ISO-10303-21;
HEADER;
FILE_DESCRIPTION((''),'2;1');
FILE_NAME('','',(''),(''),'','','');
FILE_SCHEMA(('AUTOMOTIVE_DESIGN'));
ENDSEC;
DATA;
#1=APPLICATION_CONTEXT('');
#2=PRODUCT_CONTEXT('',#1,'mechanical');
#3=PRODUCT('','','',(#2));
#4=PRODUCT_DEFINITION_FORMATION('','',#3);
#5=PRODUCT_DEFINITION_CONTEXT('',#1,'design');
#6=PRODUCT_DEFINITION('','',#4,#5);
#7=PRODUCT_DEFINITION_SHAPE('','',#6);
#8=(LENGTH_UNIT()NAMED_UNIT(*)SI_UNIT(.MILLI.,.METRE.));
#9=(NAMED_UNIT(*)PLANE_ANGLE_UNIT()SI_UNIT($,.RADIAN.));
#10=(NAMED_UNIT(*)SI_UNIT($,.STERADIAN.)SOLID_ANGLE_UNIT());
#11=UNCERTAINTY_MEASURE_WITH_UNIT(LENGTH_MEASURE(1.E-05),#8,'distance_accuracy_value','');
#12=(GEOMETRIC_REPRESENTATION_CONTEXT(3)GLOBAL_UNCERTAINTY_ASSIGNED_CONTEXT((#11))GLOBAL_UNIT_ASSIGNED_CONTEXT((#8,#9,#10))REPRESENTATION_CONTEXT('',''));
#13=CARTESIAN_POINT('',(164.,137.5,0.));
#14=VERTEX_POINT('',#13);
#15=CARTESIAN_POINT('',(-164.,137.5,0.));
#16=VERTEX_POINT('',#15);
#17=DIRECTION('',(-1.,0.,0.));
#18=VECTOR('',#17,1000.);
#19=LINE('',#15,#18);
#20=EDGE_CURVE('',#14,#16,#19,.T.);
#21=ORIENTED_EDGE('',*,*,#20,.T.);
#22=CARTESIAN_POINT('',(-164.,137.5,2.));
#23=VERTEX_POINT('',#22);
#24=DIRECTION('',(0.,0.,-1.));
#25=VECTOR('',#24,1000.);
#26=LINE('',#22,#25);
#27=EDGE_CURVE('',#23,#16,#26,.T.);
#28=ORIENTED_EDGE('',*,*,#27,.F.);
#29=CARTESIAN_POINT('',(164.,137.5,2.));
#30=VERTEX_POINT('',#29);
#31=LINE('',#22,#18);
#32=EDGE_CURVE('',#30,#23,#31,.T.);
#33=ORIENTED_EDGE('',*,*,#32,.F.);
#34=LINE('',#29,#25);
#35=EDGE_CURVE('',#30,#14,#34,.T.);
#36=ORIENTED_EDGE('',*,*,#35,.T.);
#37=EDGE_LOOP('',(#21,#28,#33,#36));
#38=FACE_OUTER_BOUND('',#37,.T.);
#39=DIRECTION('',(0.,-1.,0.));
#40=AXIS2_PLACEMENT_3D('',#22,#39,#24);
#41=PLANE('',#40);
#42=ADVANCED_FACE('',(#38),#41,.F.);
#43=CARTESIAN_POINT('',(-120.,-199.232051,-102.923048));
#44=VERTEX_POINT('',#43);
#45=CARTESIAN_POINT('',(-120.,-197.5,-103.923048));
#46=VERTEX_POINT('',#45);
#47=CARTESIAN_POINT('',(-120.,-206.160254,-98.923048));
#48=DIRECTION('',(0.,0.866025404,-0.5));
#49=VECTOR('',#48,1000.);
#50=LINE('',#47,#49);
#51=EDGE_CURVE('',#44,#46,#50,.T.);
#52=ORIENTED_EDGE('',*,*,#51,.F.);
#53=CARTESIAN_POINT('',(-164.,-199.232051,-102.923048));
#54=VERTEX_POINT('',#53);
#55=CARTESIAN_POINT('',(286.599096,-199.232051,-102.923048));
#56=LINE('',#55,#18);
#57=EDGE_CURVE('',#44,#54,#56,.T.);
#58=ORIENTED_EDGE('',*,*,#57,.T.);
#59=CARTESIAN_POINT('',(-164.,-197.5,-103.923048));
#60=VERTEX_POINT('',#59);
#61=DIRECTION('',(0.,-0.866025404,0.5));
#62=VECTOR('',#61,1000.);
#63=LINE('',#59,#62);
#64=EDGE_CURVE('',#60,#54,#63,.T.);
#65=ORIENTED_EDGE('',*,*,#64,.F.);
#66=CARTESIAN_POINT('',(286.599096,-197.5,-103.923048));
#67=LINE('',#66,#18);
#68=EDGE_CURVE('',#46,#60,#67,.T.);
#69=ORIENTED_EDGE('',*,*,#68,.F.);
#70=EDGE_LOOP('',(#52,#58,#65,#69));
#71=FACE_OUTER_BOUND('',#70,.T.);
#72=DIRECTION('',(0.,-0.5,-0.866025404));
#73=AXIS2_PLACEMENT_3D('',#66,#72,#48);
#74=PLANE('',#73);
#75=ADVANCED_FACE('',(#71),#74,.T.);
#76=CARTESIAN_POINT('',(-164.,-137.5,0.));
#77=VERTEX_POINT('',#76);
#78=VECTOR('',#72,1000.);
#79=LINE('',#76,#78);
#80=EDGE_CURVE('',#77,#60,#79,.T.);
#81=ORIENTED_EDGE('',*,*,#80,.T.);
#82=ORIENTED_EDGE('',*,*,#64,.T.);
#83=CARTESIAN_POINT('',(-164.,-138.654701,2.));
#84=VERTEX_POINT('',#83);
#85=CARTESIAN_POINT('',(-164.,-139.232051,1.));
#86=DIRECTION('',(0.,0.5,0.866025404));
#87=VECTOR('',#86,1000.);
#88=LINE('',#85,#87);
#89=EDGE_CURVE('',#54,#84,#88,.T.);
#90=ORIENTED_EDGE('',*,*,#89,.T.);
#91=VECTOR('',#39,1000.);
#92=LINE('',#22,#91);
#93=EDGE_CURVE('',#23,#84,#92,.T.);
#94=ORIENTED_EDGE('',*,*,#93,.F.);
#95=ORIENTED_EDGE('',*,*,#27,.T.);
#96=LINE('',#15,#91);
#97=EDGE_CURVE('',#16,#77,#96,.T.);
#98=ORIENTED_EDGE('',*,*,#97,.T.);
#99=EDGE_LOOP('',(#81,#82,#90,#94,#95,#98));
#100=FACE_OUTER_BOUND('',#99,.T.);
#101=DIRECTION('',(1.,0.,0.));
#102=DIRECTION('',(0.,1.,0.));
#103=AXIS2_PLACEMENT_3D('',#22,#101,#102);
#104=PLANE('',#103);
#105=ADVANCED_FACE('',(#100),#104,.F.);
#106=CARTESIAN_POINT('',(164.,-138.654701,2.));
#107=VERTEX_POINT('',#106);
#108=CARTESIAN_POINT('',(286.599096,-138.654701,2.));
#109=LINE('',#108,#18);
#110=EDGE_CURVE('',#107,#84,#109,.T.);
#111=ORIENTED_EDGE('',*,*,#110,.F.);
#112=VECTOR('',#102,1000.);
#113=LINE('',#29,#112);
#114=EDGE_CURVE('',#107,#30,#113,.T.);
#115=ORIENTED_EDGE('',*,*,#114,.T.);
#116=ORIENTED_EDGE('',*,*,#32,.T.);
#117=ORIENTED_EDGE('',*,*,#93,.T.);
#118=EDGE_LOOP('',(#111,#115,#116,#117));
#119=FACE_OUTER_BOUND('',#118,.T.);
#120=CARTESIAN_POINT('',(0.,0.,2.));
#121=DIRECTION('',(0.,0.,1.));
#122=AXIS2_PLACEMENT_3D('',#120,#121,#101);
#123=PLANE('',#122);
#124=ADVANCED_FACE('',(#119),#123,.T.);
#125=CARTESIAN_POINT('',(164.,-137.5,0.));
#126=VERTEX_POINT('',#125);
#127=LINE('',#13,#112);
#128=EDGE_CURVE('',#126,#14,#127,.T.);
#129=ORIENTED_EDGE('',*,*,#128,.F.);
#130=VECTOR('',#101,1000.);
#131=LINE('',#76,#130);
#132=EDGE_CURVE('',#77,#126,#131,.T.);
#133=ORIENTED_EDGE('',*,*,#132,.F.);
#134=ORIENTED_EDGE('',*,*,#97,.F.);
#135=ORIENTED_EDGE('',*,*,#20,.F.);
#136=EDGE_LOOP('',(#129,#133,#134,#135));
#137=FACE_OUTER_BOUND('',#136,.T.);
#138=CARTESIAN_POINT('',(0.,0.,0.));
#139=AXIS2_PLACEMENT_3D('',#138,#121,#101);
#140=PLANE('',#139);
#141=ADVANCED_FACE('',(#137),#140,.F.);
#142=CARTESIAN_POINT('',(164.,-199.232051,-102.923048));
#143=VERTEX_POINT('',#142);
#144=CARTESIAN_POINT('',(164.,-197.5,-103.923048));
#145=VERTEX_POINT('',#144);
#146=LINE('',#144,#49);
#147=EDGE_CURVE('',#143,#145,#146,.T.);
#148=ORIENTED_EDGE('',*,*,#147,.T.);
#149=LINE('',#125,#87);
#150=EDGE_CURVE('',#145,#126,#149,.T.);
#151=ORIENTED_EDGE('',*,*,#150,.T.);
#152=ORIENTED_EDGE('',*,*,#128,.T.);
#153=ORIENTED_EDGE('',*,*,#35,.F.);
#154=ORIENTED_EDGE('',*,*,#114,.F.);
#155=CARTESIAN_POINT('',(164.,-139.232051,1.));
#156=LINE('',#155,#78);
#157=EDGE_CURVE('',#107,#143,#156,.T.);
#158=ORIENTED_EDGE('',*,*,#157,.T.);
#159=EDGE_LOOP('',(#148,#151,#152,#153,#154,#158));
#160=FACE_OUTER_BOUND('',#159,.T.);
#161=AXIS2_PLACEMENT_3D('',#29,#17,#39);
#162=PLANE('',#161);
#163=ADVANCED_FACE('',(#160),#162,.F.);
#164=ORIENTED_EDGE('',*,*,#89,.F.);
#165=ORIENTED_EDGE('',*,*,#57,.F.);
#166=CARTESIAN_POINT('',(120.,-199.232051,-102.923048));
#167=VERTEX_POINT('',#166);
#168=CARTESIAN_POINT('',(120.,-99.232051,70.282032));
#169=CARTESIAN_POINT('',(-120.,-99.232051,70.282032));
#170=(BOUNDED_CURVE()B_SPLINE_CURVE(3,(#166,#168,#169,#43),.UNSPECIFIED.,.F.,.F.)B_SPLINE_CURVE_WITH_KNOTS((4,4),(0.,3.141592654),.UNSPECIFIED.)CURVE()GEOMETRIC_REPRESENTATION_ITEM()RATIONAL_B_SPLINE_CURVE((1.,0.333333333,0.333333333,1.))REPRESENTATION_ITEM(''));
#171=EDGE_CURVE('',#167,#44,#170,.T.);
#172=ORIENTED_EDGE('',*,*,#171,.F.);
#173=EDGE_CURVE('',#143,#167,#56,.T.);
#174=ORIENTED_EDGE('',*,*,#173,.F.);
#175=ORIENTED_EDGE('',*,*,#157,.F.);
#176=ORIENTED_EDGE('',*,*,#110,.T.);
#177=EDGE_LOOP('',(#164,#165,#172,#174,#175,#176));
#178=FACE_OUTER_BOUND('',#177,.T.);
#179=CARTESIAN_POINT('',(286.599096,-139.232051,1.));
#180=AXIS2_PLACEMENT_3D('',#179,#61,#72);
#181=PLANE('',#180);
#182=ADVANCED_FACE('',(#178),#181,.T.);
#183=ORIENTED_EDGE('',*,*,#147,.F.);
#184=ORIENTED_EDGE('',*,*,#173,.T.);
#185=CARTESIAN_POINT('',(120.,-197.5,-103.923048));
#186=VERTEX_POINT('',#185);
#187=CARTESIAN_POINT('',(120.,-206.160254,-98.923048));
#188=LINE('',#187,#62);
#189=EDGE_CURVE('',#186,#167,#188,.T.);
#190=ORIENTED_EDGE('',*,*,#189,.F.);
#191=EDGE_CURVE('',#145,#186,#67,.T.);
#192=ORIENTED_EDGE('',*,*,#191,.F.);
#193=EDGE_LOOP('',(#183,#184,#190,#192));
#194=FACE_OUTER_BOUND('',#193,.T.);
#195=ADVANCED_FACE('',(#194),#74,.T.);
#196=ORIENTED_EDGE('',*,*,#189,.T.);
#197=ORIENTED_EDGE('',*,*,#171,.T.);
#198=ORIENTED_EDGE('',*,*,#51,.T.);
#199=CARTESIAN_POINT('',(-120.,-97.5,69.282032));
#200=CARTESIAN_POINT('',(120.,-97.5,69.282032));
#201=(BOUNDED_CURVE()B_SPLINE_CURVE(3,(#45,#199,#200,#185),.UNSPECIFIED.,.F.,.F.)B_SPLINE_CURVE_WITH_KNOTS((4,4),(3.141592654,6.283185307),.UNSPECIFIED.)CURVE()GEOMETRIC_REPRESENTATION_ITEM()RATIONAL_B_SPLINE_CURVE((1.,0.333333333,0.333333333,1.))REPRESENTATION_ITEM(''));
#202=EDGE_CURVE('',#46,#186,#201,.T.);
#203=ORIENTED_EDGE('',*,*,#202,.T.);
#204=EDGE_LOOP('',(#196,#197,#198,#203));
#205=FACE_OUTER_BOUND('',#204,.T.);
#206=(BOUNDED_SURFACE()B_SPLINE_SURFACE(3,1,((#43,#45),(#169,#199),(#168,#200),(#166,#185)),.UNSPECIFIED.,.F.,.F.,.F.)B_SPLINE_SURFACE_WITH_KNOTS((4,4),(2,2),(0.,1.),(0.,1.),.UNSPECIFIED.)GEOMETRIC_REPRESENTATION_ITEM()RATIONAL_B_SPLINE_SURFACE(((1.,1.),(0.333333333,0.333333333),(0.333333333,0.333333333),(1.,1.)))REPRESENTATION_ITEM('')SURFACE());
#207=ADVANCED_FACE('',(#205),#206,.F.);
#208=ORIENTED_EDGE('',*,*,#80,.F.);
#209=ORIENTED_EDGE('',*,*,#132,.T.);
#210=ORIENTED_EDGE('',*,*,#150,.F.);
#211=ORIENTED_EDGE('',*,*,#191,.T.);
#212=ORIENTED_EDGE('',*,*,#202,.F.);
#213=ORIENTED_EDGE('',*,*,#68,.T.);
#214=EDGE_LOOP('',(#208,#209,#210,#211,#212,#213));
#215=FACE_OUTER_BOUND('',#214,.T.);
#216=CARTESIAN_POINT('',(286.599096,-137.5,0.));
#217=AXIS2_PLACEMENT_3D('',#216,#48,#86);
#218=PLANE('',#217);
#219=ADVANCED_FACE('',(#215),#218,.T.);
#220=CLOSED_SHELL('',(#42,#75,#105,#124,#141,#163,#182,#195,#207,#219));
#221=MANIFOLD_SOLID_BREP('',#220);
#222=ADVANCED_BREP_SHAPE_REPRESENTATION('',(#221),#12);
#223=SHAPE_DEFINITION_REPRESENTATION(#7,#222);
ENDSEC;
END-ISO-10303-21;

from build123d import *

# Parameters (mm, degrees)
SKETCH_1_W          = 328
SKETCH_1_H          = 275
EXTRUDE_1_DEPTH     = 2
EXTRUDE_2_DEPTH     = 328
SKETCH_4_RX         = 120
SKETCH_4_RY         = 100
CUT_EXTRUDE_1_DEPTH = 10


with BuildPart() as part:
    # 草图1 → 凸台-拉伸1 (new body)
    with BuildSketch(Plane.XY):
        Rectangle(SKETCH_1_W, SKETCH_1_H)
    extrude(amount=EXTRUDE_1_DEPTH)

    # 草图2 → 凸台-拉伸2 (add)
    with BuildSketch(Plane.ZY.offset(164)):
        Polygon((0, -137.5), (-103.923048454, -197.5), (-102.923048454, -199.232050808), (1, -139.232050808), (2, -138.654700538), (2, -137.5), align=None)
    extrude(amount=-EXTRUDE_2_DEPTH)

    # 草图4 → 切除-拉伸1 (cut)
    with BuildSketch(Plane(origin=(0, -103.125, 59.53924651), x_dir=(1, 0, 0), z_dir=(0, 0.8660254037844398, -0.49999999999999784))):
        with Locations(Location((0, 188.75), (0, 0, 0))):
            Ellipse(SKETCH_4_RX, SKETCH_4_RY)
    extrude(amount=-CUT_EXTRUDE_1_DEPTH, mode=Mode.SUBTRACT)


solid = part.part
